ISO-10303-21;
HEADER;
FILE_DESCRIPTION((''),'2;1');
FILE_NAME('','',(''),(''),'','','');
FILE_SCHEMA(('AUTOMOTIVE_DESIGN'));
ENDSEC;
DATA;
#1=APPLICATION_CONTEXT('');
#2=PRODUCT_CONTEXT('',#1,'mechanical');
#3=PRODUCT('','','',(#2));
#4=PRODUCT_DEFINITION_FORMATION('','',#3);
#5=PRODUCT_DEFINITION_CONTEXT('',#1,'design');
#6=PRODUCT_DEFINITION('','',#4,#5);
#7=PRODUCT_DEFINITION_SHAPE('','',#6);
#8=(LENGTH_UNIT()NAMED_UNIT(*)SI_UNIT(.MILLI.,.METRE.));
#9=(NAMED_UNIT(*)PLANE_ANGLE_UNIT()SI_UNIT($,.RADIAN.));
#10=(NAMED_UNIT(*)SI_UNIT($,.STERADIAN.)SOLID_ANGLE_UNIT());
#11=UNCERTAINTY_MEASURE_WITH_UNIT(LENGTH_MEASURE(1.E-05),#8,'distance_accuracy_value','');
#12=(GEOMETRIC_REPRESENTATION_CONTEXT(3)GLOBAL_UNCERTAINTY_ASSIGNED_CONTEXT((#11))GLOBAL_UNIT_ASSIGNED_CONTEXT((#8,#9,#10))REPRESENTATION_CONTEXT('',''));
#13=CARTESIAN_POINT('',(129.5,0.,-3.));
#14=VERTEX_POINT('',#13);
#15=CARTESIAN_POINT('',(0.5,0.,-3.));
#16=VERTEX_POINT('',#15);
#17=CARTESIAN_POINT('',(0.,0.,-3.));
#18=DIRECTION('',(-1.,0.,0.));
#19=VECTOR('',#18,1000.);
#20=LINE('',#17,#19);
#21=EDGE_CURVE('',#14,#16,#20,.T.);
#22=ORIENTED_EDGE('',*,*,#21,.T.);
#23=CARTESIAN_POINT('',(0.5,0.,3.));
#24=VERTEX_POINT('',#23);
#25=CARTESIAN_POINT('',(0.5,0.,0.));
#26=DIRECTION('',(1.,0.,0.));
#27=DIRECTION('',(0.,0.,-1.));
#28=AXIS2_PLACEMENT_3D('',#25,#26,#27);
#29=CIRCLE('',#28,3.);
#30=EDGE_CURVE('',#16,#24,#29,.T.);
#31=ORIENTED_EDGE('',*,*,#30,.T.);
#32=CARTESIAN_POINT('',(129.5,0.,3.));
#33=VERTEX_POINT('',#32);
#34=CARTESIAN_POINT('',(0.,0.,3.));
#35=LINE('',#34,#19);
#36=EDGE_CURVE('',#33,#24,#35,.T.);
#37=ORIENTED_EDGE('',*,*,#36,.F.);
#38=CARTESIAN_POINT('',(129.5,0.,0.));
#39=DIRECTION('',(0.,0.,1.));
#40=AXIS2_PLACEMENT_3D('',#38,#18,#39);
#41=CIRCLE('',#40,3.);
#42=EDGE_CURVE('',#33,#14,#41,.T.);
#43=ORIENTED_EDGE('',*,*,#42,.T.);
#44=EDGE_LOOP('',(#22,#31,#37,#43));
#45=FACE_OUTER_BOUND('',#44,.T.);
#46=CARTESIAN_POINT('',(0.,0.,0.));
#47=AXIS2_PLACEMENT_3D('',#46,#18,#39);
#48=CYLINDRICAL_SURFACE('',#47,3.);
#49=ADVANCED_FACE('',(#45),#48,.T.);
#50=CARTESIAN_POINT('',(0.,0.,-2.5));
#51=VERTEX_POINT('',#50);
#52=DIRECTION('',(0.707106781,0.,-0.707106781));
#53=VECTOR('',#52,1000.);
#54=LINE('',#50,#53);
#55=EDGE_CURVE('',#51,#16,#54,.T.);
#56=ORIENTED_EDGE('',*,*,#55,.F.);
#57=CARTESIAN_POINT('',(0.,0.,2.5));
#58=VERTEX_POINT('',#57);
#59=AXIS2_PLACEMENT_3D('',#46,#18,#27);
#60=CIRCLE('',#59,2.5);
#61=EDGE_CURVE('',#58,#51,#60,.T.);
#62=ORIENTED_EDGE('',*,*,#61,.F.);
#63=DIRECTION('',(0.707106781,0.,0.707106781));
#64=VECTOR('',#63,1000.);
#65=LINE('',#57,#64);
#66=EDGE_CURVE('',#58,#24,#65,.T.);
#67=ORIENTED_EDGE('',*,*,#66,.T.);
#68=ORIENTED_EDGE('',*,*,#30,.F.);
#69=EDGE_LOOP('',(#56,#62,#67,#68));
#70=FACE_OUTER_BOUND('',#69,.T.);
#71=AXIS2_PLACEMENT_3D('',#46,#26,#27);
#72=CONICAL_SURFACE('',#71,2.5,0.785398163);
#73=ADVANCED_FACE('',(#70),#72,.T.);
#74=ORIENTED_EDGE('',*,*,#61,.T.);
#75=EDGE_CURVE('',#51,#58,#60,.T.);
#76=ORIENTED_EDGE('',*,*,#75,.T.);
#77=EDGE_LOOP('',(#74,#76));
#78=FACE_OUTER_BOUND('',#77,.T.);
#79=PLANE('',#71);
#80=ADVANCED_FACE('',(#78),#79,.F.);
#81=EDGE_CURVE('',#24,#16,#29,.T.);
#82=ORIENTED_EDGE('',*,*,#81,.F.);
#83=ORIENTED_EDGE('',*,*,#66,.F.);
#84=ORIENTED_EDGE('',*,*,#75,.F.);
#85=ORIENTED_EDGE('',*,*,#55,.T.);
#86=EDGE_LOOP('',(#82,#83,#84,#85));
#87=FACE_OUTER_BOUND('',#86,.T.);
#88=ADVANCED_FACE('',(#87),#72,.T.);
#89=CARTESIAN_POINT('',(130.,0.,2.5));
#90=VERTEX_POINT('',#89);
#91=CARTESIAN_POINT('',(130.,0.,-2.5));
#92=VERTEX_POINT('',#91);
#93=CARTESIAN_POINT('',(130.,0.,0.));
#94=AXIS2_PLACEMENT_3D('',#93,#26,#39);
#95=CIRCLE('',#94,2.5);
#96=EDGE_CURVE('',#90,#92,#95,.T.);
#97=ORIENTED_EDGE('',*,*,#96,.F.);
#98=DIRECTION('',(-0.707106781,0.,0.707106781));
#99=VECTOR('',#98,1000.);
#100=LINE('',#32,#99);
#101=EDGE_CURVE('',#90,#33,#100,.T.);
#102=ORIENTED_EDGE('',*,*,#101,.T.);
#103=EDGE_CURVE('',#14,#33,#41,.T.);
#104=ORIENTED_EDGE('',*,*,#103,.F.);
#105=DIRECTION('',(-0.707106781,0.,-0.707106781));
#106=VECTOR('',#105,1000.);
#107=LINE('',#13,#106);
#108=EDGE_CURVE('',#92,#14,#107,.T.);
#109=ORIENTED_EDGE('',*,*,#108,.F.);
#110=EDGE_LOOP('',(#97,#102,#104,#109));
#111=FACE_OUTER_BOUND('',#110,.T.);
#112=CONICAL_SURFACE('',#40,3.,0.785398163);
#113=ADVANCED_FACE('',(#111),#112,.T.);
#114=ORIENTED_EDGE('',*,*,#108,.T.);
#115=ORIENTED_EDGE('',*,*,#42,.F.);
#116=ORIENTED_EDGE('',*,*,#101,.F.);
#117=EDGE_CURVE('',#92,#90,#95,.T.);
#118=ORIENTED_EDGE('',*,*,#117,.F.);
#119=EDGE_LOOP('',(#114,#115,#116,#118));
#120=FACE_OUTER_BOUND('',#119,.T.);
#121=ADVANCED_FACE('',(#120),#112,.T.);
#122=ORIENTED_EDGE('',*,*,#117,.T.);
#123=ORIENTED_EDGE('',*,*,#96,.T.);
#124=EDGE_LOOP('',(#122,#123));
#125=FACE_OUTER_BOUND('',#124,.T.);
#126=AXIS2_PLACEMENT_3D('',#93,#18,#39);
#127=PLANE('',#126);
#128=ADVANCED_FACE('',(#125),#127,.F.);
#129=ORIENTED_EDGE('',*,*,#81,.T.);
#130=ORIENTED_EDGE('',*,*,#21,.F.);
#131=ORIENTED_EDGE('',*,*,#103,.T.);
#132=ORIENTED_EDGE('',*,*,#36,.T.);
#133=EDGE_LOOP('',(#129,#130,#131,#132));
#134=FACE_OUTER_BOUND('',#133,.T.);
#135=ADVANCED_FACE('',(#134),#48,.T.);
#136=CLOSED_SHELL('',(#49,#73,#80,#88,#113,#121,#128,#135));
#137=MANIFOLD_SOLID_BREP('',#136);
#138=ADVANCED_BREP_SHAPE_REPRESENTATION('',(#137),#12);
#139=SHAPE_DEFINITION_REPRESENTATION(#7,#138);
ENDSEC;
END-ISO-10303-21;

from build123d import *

# Parameters (mm, degrees)
SKETCH1_W     = 130
SKETCH1_H     = 3
CHAMFER1_SIZE = 0.5


with BuildPart() as part:
    # Sketch1 → Revolve1 (revolve)
    with BuildSketch(Plane.XY, mode=Mode.PRIVATE) as revolve1_sk:
        with Locations((65, 1.5)):
            Rectangle(SKETCH1_W, SKETCH1_H)
    revolve(revolve1_sk.sketch.rotate(Axis((0, 0, 0), (1, 0, 0)), 90), axis=Axis((0, 0, 0), (1, 0, 0)))

    # Chamfer1
    chamfer1_edges = [part.edges().sort_by_distance(p)[0] for p in [
        (130, 0, -3),
        (0, 0, -3),
    ]]
    chamfer(chamfer1_edges, length=CHAMFER1_SIZE)


solid = part.part
